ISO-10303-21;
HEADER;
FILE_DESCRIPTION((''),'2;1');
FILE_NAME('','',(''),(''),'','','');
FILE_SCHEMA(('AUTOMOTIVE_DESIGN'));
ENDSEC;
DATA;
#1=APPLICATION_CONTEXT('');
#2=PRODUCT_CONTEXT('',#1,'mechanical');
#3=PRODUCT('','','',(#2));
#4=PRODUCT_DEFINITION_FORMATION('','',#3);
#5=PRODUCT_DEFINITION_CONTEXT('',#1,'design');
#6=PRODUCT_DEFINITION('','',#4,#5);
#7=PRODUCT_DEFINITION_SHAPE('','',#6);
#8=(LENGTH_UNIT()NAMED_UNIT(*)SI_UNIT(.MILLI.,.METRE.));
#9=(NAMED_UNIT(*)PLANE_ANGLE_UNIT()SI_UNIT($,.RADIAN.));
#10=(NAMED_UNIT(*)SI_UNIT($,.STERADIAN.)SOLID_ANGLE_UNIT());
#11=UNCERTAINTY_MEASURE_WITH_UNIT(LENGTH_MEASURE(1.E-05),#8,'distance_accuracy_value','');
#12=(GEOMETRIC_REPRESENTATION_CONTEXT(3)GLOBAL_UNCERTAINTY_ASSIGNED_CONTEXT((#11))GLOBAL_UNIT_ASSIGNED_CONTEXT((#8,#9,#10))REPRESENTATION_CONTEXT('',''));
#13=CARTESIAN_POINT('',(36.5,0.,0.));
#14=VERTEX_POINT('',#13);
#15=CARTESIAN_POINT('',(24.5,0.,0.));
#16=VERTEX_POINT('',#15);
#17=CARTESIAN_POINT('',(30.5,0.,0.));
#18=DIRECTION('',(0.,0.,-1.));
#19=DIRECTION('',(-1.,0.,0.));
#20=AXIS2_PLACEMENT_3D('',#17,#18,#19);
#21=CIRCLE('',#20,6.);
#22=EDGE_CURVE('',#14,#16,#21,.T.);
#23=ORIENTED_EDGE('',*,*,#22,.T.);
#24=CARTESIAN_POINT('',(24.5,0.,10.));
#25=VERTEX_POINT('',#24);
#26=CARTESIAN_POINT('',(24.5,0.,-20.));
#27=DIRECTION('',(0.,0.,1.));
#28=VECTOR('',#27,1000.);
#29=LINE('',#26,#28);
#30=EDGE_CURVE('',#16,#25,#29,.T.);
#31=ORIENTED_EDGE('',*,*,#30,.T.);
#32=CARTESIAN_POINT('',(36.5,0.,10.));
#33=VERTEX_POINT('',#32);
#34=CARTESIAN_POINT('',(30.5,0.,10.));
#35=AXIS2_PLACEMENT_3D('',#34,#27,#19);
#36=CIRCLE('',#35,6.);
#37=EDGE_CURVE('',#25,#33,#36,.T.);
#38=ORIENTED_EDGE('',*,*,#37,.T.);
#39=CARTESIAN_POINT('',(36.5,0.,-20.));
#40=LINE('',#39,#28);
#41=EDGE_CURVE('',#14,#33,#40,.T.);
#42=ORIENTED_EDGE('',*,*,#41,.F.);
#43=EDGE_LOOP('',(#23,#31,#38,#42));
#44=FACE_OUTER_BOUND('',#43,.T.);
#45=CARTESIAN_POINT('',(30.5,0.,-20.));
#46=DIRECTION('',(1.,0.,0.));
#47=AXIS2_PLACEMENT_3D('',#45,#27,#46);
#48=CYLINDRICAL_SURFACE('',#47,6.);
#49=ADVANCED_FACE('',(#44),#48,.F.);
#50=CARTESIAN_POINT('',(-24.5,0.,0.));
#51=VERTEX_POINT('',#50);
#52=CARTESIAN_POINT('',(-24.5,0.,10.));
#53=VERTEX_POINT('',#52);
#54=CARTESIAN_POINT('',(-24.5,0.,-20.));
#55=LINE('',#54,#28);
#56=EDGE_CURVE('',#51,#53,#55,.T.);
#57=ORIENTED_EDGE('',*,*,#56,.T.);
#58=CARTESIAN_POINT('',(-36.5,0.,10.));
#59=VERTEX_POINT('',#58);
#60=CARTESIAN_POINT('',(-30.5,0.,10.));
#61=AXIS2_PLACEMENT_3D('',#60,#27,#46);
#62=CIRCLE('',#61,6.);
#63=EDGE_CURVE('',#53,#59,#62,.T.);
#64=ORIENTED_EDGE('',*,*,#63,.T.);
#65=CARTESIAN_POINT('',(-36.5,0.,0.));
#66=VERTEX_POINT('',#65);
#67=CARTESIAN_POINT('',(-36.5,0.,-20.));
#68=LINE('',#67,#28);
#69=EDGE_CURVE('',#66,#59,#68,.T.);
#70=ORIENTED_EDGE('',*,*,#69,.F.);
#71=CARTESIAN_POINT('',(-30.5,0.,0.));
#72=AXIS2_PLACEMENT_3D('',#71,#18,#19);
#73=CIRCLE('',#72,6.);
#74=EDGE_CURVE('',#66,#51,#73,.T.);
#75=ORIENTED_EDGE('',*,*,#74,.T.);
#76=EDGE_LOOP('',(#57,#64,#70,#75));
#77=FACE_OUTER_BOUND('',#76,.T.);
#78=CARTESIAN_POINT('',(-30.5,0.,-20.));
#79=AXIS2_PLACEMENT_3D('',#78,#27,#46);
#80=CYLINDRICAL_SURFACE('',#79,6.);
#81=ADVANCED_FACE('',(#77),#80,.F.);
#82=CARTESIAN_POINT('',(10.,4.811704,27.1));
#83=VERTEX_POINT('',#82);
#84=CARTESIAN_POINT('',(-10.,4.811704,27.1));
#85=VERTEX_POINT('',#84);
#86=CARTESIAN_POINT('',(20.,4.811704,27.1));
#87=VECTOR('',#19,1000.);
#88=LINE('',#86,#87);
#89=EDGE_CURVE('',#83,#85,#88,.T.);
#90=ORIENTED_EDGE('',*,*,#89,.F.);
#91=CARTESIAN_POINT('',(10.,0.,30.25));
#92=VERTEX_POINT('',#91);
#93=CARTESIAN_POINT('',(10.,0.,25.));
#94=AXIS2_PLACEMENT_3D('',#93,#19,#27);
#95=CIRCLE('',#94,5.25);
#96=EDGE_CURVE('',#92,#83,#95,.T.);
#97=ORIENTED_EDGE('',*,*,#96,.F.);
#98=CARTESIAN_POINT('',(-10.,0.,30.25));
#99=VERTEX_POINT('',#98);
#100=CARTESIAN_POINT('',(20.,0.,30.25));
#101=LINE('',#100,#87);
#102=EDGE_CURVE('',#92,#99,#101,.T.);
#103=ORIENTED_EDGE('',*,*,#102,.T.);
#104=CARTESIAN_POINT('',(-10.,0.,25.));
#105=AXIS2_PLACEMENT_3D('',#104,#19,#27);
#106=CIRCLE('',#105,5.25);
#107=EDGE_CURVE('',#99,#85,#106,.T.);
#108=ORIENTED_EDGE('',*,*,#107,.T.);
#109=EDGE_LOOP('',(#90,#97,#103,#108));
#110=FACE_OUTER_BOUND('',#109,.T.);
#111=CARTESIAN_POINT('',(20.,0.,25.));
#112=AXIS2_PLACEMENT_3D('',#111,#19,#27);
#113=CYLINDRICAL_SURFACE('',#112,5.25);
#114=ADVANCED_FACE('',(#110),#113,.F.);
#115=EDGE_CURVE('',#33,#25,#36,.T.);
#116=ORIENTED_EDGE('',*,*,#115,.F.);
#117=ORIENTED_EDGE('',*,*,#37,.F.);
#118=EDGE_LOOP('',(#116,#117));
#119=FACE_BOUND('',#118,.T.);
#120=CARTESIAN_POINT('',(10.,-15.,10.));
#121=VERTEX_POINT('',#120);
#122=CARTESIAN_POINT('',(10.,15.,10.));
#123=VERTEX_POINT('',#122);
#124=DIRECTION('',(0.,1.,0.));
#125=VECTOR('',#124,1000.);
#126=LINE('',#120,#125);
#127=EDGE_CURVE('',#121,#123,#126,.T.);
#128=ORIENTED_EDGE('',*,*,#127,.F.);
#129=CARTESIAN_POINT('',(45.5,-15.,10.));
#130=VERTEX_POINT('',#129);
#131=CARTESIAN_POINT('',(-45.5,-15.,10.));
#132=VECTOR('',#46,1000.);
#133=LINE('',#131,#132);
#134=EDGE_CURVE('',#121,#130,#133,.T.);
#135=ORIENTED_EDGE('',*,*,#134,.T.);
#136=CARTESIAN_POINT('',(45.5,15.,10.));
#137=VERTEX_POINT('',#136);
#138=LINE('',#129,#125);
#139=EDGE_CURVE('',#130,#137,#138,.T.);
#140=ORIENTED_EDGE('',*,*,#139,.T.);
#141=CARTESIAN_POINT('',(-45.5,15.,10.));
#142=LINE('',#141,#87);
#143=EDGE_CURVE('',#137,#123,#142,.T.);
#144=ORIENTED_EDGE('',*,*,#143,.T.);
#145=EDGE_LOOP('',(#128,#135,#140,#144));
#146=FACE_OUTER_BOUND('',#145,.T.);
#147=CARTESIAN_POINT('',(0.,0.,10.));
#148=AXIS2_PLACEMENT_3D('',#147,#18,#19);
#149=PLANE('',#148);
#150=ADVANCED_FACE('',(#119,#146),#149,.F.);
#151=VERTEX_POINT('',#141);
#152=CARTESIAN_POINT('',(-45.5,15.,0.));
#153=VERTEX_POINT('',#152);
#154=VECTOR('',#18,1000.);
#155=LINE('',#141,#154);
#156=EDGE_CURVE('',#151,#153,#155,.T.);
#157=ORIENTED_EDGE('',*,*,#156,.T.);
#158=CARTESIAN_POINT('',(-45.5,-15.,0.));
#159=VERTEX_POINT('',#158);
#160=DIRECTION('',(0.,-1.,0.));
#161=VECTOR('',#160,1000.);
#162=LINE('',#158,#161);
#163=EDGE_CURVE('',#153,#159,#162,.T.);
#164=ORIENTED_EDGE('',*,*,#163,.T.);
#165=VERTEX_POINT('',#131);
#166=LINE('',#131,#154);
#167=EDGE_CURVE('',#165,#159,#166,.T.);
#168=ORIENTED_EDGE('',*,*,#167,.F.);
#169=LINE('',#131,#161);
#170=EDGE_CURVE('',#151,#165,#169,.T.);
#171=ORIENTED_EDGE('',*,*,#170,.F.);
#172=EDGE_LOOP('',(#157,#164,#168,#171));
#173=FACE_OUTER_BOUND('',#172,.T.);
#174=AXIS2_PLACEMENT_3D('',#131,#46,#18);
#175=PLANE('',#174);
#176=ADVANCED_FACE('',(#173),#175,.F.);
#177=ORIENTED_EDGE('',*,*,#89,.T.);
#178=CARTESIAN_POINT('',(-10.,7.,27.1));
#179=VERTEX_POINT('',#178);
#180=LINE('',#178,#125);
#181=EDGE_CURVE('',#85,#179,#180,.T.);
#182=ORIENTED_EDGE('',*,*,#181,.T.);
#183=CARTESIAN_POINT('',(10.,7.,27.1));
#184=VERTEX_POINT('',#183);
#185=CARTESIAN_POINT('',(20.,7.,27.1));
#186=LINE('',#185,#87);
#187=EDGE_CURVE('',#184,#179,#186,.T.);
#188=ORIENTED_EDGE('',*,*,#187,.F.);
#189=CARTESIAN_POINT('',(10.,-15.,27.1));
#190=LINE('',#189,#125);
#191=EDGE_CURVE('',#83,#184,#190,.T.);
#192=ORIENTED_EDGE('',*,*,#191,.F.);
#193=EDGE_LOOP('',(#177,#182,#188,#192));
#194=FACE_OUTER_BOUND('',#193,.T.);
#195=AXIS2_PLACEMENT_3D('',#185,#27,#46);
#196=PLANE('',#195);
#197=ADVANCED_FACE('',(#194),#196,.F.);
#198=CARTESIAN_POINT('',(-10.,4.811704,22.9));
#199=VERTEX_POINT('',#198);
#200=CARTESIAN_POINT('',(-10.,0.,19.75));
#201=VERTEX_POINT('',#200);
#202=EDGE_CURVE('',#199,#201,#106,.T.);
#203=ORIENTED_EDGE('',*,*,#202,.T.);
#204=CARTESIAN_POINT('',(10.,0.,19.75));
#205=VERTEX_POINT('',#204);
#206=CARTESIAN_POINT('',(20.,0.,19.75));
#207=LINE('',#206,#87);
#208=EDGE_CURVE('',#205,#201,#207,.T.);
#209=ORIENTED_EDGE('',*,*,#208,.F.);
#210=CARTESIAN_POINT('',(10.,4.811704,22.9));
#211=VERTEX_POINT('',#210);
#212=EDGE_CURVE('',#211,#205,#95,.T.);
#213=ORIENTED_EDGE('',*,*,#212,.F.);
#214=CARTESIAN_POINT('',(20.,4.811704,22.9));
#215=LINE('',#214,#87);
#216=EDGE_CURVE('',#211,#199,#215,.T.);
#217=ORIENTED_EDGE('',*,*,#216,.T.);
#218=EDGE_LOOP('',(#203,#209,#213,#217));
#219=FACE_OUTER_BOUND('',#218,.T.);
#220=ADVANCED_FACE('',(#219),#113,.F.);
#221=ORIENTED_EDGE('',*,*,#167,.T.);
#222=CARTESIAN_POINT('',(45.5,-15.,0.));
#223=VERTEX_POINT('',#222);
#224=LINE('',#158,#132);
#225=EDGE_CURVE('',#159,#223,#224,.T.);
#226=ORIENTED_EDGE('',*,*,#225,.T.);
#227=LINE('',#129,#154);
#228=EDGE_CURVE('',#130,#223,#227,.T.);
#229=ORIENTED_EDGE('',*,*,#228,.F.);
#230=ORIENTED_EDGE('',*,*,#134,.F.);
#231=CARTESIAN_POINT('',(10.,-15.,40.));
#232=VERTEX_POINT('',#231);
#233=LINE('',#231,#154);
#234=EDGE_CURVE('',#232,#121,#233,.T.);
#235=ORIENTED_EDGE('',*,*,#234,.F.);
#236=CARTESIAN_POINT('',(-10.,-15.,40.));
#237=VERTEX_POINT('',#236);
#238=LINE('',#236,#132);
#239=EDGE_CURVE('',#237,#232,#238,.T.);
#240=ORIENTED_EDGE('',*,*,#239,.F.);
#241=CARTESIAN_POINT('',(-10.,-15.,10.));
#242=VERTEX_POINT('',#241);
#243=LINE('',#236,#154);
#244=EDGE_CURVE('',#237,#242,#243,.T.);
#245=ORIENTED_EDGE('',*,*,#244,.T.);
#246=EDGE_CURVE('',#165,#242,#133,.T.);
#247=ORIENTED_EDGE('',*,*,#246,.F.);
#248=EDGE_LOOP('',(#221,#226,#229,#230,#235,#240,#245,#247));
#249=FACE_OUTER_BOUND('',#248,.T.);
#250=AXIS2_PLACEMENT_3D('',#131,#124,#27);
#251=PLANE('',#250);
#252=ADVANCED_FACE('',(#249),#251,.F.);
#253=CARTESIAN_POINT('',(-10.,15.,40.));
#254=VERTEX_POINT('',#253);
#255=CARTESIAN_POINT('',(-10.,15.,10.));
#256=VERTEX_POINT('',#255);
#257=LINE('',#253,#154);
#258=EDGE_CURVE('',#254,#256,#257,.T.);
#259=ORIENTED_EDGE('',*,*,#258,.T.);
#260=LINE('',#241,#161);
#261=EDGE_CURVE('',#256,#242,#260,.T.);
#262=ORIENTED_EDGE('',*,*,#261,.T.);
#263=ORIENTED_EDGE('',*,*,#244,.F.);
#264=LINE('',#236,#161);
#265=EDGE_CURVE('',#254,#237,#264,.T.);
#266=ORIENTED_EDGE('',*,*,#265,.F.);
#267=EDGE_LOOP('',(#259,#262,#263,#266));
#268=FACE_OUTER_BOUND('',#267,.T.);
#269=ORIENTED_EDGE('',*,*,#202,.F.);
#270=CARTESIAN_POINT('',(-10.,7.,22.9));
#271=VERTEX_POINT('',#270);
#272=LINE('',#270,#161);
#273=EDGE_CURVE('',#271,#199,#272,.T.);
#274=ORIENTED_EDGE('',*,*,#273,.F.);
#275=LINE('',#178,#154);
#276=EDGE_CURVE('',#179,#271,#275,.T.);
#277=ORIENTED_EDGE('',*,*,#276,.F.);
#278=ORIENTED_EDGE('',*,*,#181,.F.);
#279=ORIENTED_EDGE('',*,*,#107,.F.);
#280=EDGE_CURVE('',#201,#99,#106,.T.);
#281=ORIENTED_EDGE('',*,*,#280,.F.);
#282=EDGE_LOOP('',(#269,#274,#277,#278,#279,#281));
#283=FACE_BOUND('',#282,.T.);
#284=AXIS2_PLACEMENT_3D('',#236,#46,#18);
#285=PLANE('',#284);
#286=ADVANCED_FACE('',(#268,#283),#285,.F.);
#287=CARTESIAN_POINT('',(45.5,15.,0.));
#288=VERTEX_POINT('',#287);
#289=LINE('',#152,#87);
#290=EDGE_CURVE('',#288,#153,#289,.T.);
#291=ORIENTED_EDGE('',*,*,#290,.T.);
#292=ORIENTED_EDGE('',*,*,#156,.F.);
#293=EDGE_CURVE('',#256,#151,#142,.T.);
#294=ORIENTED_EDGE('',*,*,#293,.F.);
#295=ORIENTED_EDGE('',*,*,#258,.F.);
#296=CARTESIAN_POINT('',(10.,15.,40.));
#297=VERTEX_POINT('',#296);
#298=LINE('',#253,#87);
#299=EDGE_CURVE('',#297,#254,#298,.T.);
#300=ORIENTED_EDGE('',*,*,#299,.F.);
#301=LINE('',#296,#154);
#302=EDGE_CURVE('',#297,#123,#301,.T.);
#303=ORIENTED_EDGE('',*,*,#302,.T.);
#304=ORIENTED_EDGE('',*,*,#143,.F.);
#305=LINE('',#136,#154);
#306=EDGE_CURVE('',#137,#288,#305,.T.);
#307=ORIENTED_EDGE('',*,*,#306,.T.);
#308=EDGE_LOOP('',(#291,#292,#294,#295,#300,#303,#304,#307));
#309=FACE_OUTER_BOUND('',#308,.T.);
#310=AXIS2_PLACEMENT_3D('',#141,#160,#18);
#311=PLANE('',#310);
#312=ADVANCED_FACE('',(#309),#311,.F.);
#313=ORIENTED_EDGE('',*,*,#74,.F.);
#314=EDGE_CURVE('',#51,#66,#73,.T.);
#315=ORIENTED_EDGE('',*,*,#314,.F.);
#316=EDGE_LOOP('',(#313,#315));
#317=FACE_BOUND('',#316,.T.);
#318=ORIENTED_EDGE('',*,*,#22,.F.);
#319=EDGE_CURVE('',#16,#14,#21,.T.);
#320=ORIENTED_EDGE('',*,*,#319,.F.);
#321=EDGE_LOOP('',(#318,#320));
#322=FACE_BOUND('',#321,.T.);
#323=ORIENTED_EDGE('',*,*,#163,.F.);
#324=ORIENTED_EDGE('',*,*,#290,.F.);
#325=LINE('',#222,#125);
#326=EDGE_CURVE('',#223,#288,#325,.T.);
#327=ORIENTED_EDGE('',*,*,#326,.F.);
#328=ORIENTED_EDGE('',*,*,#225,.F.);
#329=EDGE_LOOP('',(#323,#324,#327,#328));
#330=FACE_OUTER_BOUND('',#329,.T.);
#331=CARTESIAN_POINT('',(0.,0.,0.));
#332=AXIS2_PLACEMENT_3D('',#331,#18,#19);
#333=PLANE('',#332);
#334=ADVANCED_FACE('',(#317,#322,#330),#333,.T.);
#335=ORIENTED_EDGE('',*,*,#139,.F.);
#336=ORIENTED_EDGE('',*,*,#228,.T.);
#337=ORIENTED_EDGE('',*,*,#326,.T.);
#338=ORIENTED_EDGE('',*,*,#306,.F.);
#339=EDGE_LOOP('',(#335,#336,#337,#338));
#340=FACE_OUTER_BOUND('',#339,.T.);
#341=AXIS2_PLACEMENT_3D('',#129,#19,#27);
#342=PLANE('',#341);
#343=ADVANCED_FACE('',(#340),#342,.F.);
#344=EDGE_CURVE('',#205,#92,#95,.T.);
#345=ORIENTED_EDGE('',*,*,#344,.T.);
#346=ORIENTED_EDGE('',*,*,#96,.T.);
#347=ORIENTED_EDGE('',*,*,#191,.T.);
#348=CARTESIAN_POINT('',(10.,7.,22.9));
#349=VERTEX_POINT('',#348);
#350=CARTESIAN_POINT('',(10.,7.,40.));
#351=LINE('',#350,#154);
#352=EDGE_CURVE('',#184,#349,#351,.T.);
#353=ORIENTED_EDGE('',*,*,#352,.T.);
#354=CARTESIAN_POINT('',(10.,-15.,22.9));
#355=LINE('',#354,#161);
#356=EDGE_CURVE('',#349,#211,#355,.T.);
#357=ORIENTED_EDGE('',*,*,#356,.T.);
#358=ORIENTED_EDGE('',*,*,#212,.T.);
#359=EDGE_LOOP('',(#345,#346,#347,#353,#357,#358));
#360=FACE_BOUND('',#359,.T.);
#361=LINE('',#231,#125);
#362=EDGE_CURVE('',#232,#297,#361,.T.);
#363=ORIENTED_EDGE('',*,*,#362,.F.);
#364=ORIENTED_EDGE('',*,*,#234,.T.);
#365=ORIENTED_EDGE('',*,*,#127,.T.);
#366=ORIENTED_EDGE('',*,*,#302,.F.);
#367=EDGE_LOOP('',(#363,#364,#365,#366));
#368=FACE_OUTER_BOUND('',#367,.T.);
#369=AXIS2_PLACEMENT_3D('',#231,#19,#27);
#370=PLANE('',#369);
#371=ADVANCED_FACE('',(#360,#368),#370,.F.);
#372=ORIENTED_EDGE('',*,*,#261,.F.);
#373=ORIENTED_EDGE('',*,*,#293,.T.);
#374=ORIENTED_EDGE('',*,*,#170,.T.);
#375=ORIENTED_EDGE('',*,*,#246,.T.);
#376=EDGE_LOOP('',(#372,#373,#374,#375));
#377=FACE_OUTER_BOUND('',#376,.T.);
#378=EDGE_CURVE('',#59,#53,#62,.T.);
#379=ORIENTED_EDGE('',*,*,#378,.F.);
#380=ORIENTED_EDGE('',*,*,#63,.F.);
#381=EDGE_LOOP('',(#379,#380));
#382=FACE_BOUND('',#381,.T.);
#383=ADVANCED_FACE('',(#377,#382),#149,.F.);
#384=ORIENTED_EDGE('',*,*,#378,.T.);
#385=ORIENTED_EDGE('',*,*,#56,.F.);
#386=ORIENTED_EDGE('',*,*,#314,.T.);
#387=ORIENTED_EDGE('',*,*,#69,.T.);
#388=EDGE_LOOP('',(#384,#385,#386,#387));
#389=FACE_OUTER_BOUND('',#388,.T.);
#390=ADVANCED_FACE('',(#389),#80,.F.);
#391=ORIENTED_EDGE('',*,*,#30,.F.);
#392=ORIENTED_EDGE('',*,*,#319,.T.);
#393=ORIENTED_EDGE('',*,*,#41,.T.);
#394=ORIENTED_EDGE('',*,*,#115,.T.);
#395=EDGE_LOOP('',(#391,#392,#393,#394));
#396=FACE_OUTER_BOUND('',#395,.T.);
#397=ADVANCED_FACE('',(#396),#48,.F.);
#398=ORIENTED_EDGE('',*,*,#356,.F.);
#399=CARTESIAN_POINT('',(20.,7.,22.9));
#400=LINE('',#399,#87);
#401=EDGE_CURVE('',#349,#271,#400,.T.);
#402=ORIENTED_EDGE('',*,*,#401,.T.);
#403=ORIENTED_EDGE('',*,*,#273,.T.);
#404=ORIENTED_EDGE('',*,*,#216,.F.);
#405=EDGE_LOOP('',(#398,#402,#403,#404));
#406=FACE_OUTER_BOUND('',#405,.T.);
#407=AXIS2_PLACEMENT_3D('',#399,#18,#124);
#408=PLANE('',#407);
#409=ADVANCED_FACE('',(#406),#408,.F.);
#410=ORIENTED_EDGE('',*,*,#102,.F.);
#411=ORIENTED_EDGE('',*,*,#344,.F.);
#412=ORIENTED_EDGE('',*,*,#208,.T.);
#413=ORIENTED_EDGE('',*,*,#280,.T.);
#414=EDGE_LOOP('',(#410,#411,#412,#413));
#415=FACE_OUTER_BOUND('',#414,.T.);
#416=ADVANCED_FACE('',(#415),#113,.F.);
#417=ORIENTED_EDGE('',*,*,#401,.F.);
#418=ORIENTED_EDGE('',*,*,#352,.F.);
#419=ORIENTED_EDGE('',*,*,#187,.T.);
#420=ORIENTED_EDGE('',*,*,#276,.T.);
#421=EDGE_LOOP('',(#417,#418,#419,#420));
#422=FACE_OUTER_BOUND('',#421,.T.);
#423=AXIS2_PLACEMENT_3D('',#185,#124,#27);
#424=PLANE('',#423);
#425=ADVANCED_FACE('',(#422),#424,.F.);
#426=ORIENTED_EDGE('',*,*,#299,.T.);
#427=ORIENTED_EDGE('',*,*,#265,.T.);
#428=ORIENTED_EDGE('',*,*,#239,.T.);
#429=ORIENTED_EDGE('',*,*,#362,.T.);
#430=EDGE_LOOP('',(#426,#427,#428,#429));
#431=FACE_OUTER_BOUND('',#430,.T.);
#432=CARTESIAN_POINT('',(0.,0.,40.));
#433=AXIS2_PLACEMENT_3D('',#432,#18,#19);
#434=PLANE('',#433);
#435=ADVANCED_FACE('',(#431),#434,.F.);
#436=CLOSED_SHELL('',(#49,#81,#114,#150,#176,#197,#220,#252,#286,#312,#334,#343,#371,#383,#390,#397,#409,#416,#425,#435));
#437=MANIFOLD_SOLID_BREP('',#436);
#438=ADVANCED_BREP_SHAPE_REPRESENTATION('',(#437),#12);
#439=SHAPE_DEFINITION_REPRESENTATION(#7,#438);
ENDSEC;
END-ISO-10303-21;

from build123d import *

# Parameters (mm, degrees)
SKETCH1_W           = 91
SKETCH1_H           = 30
BOSS_EXTRUDE1_DEPTH = 10
SKETCH2_W           = 20
SKETCH2_H           = 30
BOSS_EXTRUDE2_DEPTH = 30
CUT_EXTRUDE1_DEPTH  = 30
SKETCH5_R           = 6
CUT_EXTRUDE2_DEPTH  = 30


with BuildPart() as part:
    # Sketch1 → Boss-Extrude1 (new body)
    with BuildSketch(Plane.XY):
        Rectangle(SKETCH1_W, SKETCH1_H)
    extrude(amount=BOSS_EXTRUDE1_DEPTH)

    # Sketch2 → Boss-Extrude2 (add)
    with BuildSketch(Plane.XY.offset(10)):
        Rectangle(SKETCH2_W, SKETCH2_H)
    extrude(amount=BOSS_EXTRUDE2_DEPTH)

    # Sketch4 → Cut-Extrude1 (cut)
    with BuildSketch(Plane.ZY.offset(10)):
        with BuildLine():
            Line((27.1, 7), (22.9, 7))
            Line((22.9, 7), (22.9, 4.81170448))
            ThreePointArc((22.9, 4.81170448), (25, -5.25), (27.1, 4.81170448))
            Line((27.1, 4.81170448), (27.1, 7))
        make_face()
    extrude(amount=-CUT_EXTRUDE1_DEPTH, mode=Mode.SUBTRACT)

    # Sketch5 → Cut-Extrude2 (cut)
    with BuildSketch(Plane.XY.offset(10)):
        with Locations((-30.5, 0)):
            Circle(SKETCH5_R)
        with Locations(Location((30.5, 0, 0), (0, 0, 180))):
            Circle(SKETCH5_R)
    extrude(amount=-CUT_EXTRUDE2_DEPTH, mode=Mode.SUBTRACT)


solid = part.part
